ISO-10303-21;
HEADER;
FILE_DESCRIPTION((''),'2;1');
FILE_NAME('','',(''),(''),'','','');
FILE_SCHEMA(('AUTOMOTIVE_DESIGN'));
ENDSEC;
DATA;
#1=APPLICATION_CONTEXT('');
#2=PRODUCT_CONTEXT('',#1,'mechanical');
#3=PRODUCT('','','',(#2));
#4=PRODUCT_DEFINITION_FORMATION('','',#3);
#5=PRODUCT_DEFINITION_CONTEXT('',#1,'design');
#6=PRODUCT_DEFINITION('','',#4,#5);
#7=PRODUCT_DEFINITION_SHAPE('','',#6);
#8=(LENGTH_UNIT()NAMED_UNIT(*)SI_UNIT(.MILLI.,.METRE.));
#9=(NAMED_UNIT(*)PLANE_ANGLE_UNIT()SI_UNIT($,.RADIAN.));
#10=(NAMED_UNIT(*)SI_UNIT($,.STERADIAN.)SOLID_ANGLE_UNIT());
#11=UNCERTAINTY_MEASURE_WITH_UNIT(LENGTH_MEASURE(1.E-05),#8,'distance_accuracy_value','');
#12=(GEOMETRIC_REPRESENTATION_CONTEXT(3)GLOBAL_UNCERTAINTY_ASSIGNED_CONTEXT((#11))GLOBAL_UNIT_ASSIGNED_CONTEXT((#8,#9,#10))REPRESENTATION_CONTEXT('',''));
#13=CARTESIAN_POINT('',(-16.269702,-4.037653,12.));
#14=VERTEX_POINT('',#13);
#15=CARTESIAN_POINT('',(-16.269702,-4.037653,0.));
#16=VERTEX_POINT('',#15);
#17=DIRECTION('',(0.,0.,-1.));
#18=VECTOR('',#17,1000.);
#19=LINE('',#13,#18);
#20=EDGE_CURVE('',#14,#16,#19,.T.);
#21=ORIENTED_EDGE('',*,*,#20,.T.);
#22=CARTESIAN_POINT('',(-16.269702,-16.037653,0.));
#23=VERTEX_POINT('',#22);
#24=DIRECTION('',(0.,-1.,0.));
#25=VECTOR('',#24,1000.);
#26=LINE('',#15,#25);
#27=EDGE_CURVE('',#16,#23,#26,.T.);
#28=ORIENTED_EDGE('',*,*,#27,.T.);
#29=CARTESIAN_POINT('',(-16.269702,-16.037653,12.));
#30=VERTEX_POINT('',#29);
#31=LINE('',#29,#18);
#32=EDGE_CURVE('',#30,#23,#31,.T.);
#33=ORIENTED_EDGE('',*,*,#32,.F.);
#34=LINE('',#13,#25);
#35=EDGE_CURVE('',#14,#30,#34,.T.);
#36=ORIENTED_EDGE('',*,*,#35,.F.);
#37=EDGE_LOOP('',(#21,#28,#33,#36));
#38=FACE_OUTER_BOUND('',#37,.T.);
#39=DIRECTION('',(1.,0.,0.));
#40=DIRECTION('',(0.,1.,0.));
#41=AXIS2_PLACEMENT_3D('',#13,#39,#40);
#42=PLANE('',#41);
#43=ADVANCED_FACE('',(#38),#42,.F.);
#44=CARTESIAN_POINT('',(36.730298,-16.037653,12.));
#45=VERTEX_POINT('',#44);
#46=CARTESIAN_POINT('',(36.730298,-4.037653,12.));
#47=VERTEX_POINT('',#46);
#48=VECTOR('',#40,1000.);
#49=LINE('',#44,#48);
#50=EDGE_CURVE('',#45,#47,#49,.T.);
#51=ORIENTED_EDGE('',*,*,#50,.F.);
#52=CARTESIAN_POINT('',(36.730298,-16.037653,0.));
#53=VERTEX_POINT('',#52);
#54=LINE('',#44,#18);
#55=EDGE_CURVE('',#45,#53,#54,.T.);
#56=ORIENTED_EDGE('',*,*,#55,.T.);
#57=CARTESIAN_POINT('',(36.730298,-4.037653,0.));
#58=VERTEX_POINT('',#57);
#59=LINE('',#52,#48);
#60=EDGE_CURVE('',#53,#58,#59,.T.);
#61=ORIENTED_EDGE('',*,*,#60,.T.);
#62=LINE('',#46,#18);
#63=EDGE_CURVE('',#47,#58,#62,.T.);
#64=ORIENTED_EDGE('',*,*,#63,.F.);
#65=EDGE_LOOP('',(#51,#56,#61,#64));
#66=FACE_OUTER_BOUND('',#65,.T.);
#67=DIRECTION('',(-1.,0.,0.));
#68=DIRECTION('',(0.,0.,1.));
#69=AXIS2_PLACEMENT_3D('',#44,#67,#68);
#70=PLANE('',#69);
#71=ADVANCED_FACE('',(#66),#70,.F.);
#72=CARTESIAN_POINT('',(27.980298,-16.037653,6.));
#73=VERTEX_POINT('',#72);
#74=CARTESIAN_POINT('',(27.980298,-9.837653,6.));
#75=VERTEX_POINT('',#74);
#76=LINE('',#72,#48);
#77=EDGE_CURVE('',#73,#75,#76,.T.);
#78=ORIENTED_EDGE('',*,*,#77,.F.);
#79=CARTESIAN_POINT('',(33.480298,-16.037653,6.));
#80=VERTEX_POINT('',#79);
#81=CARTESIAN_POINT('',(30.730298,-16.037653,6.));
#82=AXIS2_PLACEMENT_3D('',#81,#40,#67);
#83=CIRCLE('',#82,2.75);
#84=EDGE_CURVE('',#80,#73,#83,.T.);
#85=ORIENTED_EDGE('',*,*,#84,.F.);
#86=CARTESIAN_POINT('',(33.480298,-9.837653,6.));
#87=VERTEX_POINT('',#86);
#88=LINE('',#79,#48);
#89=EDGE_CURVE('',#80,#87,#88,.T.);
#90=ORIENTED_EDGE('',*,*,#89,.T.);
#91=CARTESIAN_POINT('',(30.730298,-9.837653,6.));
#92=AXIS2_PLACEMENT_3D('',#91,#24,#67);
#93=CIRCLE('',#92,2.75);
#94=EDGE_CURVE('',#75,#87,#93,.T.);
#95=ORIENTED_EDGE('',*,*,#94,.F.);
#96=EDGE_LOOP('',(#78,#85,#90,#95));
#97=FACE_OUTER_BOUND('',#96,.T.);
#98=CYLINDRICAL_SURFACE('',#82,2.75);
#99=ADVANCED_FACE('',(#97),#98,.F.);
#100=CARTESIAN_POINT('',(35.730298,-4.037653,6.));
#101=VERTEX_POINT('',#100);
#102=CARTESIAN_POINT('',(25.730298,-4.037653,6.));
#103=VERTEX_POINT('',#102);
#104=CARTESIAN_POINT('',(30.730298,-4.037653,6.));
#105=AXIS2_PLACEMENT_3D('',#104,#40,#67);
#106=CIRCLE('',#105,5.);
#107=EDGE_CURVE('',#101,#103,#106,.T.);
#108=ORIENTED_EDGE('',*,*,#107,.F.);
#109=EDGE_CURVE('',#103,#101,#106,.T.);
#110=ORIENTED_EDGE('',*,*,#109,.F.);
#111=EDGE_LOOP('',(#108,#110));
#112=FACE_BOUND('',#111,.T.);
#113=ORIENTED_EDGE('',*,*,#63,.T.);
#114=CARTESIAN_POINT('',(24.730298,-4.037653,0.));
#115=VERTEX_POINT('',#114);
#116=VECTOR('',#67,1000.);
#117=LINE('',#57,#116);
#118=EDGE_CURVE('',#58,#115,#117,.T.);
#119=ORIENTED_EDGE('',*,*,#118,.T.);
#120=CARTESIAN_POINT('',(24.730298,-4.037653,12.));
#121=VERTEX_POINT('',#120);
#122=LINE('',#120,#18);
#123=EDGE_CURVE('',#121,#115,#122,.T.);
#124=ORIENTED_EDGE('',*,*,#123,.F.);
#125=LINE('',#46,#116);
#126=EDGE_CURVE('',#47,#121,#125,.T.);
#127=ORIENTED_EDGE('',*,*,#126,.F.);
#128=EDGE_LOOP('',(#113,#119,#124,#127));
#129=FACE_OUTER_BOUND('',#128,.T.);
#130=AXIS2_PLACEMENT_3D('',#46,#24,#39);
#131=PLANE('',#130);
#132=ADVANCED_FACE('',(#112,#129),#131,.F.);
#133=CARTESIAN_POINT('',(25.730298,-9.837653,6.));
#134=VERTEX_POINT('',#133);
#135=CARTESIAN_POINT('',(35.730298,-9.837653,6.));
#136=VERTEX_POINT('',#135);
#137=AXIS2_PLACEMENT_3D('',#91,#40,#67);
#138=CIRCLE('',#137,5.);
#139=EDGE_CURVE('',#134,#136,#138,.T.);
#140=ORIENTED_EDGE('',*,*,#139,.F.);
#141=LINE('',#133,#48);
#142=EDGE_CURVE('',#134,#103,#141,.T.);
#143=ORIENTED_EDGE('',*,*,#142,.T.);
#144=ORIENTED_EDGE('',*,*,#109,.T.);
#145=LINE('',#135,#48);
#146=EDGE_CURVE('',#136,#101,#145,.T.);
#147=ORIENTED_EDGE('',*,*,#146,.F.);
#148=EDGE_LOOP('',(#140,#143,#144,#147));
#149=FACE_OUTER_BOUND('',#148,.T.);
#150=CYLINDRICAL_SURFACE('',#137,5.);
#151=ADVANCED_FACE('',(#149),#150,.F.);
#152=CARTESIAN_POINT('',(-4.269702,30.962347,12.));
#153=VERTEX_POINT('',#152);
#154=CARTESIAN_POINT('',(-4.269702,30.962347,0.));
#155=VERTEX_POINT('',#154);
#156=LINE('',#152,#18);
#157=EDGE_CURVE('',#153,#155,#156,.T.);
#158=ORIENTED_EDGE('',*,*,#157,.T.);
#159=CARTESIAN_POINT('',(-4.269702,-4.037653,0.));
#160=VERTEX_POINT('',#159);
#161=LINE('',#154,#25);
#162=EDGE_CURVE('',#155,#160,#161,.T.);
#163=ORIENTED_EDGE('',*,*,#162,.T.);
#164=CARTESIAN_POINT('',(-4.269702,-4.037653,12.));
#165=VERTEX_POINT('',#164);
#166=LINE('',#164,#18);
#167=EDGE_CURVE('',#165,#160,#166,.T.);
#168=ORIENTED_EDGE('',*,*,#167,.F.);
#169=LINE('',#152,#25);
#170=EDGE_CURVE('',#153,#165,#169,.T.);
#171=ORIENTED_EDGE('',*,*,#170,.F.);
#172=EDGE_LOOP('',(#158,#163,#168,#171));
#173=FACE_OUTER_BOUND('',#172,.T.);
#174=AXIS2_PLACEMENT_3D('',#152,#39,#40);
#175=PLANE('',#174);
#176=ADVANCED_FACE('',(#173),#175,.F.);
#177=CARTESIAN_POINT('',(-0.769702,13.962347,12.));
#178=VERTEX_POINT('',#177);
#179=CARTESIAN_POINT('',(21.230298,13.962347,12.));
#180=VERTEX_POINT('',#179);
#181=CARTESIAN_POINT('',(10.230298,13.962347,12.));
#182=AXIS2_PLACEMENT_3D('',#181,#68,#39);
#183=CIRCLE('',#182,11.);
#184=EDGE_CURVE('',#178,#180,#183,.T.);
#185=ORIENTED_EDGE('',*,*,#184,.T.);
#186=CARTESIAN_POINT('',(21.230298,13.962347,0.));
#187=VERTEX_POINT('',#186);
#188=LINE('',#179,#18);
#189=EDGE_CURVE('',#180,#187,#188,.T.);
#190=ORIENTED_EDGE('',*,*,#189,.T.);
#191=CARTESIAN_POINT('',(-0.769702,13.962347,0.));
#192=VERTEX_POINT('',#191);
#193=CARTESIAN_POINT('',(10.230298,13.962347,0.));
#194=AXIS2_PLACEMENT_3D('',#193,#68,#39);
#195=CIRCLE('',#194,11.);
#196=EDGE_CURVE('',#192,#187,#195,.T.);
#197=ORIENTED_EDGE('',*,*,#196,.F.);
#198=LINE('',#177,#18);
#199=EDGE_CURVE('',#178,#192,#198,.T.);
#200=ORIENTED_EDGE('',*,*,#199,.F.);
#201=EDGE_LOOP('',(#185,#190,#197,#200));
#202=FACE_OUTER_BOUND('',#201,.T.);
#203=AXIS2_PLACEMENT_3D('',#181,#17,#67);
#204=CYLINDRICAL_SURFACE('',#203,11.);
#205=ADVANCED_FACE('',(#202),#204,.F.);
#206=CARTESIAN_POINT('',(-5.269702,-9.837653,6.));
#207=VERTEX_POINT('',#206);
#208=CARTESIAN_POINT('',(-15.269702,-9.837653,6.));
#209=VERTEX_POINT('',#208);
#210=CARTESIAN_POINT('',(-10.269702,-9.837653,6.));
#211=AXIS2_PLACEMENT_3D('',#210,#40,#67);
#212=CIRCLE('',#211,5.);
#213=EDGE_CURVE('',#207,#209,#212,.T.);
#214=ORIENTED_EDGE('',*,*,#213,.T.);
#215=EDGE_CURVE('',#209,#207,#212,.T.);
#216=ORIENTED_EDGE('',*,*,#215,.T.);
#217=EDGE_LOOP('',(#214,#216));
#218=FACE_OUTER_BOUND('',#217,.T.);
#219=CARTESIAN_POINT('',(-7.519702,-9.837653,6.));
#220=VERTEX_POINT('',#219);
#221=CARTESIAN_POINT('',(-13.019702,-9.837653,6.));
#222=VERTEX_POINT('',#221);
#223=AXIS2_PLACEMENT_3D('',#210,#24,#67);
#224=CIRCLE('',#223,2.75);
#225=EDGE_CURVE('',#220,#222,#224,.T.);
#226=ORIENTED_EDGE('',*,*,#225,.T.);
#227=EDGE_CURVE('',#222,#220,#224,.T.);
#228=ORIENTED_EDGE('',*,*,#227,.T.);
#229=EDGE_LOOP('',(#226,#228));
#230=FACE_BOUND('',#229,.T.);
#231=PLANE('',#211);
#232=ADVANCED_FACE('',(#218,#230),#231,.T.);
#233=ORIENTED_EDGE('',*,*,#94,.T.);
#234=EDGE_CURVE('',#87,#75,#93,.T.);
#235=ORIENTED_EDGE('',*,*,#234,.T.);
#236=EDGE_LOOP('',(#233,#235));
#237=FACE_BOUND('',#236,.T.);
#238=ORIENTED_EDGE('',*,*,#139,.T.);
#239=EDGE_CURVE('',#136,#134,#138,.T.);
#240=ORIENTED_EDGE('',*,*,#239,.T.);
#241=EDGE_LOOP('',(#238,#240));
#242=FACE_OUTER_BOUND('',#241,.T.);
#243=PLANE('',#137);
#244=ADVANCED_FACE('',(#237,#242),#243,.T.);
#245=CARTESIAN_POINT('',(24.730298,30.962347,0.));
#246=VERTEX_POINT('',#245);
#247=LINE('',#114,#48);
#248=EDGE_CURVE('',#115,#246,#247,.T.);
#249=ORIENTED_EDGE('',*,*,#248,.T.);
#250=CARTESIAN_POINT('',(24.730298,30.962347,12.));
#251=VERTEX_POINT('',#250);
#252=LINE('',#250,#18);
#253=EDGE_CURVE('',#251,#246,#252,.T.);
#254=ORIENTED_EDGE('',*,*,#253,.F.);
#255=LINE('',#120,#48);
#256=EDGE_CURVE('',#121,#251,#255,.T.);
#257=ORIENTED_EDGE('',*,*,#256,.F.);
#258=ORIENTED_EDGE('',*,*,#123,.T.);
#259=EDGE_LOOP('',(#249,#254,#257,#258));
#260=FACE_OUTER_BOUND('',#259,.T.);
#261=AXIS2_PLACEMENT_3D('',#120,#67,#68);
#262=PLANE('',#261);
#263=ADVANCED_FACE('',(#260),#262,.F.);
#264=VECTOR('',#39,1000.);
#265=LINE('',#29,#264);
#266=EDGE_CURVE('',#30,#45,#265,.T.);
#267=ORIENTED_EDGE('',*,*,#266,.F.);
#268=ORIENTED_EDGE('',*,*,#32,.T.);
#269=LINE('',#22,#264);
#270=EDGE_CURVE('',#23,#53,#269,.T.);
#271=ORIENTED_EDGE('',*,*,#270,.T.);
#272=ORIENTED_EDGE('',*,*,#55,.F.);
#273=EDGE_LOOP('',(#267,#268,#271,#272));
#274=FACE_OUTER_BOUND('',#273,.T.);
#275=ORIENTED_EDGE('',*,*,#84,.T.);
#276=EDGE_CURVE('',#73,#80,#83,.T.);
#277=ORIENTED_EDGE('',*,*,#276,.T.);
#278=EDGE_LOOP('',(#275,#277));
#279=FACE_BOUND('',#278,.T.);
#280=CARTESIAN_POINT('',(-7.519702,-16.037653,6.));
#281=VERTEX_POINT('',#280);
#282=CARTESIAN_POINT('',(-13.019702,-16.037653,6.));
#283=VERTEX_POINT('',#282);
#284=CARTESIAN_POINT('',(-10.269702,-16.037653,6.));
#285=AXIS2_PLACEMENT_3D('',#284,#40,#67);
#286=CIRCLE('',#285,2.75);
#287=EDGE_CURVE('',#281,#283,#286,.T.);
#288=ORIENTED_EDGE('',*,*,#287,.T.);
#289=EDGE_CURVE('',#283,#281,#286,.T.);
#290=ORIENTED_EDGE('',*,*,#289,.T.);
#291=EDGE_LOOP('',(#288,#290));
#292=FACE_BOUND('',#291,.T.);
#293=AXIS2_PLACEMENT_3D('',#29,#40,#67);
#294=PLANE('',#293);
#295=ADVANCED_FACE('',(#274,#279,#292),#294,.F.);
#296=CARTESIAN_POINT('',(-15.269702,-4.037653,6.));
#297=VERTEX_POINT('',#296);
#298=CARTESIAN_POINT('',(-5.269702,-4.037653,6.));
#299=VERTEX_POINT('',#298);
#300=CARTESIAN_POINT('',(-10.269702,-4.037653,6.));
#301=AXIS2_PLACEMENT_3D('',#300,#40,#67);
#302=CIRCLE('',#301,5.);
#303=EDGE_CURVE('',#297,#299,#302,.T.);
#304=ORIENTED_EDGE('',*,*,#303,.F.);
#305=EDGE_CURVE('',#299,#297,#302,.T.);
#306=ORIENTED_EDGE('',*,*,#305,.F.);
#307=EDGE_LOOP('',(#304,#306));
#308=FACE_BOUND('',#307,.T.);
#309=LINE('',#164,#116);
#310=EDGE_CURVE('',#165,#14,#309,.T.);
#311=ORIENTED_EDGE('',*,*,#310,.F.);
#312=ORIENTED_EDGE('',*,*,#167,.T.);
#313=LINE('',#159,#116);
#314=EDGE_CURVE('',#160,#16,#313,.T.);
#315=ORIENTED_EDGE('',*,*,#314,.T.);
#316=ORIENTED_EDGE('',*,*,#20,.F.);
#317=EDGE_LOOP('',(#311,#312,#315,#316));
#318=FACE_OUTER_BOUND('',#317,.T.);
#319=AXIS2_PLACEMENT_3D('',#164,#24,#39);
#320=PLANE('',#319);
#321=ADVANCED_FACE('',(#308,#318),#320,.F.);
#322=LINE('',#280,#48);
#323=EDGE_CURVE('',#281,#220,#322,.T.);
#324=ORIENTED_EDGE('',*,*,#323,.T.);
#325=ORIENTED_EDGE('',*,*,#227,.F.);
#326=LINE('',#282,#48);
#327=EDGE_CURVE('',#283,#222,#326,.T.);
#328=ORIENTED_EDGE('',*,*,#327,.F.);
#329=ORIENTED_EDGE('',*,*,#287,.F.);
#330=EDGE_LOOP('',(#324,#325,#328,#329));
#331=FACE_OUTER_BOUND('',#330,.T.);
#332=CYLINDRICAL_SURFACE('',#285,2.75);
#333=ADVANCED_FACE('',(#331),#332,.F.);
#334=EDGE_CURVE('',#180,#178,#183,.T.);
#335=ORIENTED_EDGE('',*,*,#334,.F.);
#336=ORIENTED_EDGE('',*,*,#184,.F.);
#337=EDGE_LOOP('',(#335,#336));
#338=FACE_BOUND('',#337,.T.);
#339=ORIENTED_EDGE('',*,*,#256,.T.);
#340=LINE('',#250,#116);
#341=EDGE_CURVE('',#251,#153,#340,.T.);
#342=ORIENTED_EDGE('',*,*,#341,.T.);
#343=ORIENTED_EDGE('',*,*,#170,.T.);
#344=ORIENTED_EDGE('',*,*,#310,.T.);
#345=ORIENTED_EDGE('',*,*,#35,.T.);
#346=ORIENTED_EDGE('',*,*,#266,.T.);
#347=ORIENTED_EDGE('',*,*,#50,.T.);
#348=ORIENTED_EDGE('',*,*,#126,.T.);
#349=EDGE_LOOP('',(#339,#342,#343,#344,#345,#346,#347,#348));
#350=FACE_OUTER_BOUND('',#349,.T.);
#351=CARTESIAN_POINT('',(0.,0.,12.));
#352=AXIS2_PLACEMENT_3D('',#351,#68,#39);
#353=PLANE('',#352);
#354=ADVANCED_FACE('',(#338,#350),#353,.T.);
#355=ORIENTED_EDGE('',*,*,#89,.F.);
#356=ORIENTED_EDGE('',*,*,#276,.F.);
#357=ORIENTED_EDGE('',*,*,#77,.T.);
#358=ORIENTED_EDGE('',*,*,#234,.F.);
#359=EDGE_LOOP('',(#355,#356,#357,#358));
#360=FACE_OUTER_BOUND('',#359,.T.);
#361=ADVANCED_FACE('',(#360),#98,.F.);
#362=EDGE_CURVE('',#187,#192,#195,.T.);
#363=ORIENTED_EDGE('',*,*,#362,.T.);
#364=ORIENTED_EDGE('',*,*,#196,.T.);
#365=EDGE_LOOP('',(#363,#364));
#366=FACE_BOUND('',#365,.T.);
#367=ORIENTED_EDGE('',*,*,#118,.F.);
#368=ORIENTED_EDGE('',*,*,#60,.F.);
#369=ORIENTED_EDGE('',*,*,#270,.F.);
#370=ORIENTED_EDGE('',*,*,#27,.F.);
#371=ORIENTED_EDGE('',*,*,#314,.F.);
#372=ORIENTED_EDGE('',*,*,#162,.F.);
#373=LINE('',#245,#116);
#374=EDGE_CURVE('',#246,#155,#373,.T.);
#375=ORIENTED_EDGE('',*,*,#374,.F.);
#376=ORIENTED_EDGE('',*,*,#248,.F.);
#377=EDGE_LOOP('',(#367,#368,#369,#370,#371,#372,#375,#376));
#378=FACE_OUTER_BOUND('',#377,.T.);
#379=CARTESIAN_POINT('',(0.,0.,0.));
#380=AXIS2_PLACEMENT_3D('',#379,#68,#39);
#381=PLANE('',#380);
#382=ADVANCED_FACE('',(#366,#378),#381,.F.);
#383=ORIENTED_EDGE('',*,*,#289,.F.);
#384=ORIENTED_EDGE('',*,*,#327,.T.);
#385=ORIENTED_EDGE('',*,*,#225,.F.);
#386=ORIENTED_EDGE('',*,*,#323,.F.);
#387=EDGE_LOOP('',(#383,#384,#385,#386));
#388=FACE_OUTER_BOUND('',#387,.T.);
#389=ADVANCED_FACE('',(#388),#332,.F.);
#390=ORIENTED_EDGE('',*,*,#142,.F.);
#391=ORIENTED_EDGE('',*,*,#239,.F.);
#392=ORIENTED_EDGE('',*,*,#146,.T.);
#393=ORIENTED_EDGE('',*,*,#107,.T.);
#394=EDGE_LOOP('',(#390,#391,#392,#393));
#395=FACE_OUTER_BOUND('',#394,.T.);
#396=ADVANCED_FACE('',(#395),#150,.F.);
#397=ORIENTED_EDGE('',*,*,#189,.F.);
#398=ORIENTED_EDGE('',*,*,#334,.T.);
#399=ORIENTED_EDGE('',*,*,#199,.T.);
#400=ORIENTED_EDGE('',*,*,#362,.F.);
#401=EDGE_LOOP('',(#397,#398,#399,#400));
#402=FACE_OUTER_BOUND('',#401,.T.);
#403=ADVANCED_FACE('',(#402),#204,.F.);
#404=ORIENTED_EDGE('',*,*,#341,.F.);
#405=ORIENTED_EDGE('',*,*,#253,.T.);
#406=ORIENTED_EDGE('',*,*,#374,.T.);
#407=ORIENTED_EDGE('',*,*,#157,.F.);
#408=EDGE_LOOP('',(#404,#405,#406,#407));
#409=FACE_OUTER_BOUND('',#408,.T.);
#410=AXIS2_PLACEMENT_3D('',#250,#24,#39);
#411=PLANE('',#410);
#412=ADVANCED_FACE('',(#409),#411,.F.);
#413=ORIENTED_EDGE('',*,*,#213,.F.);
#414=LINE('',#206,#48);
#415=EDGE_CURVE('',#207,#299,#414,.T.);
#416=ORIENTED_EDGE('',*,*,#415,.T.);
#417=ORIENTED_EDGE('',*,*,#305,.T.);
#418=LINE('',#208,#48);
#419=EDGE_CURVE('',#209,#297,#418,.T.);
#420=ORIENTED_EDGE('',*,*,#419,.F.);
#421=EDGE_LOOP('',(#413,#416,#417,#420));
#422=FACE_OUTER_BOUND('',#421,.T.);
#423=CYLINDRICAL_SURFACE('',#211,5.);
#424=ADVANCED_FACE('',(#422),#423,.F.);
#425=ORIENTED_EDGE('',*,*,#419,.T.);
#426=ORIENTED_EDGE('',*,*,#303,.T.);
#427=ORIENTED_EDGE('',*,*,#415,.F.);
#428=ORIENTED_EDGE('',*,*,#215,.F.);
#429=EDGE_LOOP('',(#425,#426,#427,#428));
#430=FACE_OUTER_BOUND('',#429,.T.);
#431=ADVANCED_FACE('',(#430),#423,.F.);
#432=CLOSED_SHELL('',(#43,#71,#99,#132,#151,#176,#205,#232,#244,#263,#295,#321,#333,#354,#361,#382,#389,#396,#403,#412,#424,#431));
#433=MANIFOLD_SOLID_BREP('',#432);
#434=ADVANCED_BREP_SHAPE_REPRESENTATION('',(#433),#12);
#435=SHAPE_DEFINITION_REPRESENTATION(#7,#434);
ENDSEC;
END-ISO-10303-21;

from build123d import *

# Parameters (mm, degrees)
SKETCH_1_R          = 11
EXTRUDE_1_DEPTH     = 12
SKETCH_2_R          = 2.75
CUT_EXTRUDE_1_DEPTH = 53.135542299
SKETCH_3_R          = 5
CUT_EXTRUDE_2_DEPTH = 5.8


with BuildPart() as part:
    # 草图1 → 凸台-拉伸1 (new body)
    with BuildSketch(Plane.XY):
        Polygon((-16.269702277, -16.03765324), (36.730297723, -16.03765324), (36.730297723, -4.03765324), (24.730297723, -4.03765324), (24.730297723, 30.96234676), (-4.269702277, 30.96234676), (-4.269702277, -4.03765324), (-16.269702277, -4.03765324), align=None)
        with Locations((10.230297723, 13.96234676)):
            Circle(SKETCH_1_R, mode=Mode.SUBTRACT)
    extrude(amount=EXTRUDE_1_DEPTH)

    # 草图2 → 切除-拉伸1 (cut, through all)
    with BuildSketch(Plane(origin=(0, -4.03765324, 0), x_dir=(1, 0, 0), z_dir=(0, 1, 0))):
        with Locations(Location((-10.269702277, -6, 0), (0, 0, 180))):
            Circle(SKETCH_2_R)
        with Locations(Location((30.730297723, -6, 0), (0, 0, 180))):
            Circle(SKETCH_2_R)
    extrude(amount=-CUT_EXTRUDE_1_DEPTH, mode=Mode.SUBTRACT)

    # 草图3 → 切除-拉伸2 (cut)
    with BuildSketch(Plane(origin=(0, -4.03765324, 0), x_dir=(1, 0, 0), z_dir=(0, 1, 0))):
        with Locations(Location((-10.269702277, -6, 0), (0, 0, 180))):
            Circle(SKETCH_3_R)
        with Locations(Location((30.730297723, -6, 0), (0, 0, 180))):
            Circle(SKETCH_3_R)
    extrude(amount=-CUT_EXTRUDE_2_DEPTH, mode=Mode.SUBTRACT)


solid = part.part
